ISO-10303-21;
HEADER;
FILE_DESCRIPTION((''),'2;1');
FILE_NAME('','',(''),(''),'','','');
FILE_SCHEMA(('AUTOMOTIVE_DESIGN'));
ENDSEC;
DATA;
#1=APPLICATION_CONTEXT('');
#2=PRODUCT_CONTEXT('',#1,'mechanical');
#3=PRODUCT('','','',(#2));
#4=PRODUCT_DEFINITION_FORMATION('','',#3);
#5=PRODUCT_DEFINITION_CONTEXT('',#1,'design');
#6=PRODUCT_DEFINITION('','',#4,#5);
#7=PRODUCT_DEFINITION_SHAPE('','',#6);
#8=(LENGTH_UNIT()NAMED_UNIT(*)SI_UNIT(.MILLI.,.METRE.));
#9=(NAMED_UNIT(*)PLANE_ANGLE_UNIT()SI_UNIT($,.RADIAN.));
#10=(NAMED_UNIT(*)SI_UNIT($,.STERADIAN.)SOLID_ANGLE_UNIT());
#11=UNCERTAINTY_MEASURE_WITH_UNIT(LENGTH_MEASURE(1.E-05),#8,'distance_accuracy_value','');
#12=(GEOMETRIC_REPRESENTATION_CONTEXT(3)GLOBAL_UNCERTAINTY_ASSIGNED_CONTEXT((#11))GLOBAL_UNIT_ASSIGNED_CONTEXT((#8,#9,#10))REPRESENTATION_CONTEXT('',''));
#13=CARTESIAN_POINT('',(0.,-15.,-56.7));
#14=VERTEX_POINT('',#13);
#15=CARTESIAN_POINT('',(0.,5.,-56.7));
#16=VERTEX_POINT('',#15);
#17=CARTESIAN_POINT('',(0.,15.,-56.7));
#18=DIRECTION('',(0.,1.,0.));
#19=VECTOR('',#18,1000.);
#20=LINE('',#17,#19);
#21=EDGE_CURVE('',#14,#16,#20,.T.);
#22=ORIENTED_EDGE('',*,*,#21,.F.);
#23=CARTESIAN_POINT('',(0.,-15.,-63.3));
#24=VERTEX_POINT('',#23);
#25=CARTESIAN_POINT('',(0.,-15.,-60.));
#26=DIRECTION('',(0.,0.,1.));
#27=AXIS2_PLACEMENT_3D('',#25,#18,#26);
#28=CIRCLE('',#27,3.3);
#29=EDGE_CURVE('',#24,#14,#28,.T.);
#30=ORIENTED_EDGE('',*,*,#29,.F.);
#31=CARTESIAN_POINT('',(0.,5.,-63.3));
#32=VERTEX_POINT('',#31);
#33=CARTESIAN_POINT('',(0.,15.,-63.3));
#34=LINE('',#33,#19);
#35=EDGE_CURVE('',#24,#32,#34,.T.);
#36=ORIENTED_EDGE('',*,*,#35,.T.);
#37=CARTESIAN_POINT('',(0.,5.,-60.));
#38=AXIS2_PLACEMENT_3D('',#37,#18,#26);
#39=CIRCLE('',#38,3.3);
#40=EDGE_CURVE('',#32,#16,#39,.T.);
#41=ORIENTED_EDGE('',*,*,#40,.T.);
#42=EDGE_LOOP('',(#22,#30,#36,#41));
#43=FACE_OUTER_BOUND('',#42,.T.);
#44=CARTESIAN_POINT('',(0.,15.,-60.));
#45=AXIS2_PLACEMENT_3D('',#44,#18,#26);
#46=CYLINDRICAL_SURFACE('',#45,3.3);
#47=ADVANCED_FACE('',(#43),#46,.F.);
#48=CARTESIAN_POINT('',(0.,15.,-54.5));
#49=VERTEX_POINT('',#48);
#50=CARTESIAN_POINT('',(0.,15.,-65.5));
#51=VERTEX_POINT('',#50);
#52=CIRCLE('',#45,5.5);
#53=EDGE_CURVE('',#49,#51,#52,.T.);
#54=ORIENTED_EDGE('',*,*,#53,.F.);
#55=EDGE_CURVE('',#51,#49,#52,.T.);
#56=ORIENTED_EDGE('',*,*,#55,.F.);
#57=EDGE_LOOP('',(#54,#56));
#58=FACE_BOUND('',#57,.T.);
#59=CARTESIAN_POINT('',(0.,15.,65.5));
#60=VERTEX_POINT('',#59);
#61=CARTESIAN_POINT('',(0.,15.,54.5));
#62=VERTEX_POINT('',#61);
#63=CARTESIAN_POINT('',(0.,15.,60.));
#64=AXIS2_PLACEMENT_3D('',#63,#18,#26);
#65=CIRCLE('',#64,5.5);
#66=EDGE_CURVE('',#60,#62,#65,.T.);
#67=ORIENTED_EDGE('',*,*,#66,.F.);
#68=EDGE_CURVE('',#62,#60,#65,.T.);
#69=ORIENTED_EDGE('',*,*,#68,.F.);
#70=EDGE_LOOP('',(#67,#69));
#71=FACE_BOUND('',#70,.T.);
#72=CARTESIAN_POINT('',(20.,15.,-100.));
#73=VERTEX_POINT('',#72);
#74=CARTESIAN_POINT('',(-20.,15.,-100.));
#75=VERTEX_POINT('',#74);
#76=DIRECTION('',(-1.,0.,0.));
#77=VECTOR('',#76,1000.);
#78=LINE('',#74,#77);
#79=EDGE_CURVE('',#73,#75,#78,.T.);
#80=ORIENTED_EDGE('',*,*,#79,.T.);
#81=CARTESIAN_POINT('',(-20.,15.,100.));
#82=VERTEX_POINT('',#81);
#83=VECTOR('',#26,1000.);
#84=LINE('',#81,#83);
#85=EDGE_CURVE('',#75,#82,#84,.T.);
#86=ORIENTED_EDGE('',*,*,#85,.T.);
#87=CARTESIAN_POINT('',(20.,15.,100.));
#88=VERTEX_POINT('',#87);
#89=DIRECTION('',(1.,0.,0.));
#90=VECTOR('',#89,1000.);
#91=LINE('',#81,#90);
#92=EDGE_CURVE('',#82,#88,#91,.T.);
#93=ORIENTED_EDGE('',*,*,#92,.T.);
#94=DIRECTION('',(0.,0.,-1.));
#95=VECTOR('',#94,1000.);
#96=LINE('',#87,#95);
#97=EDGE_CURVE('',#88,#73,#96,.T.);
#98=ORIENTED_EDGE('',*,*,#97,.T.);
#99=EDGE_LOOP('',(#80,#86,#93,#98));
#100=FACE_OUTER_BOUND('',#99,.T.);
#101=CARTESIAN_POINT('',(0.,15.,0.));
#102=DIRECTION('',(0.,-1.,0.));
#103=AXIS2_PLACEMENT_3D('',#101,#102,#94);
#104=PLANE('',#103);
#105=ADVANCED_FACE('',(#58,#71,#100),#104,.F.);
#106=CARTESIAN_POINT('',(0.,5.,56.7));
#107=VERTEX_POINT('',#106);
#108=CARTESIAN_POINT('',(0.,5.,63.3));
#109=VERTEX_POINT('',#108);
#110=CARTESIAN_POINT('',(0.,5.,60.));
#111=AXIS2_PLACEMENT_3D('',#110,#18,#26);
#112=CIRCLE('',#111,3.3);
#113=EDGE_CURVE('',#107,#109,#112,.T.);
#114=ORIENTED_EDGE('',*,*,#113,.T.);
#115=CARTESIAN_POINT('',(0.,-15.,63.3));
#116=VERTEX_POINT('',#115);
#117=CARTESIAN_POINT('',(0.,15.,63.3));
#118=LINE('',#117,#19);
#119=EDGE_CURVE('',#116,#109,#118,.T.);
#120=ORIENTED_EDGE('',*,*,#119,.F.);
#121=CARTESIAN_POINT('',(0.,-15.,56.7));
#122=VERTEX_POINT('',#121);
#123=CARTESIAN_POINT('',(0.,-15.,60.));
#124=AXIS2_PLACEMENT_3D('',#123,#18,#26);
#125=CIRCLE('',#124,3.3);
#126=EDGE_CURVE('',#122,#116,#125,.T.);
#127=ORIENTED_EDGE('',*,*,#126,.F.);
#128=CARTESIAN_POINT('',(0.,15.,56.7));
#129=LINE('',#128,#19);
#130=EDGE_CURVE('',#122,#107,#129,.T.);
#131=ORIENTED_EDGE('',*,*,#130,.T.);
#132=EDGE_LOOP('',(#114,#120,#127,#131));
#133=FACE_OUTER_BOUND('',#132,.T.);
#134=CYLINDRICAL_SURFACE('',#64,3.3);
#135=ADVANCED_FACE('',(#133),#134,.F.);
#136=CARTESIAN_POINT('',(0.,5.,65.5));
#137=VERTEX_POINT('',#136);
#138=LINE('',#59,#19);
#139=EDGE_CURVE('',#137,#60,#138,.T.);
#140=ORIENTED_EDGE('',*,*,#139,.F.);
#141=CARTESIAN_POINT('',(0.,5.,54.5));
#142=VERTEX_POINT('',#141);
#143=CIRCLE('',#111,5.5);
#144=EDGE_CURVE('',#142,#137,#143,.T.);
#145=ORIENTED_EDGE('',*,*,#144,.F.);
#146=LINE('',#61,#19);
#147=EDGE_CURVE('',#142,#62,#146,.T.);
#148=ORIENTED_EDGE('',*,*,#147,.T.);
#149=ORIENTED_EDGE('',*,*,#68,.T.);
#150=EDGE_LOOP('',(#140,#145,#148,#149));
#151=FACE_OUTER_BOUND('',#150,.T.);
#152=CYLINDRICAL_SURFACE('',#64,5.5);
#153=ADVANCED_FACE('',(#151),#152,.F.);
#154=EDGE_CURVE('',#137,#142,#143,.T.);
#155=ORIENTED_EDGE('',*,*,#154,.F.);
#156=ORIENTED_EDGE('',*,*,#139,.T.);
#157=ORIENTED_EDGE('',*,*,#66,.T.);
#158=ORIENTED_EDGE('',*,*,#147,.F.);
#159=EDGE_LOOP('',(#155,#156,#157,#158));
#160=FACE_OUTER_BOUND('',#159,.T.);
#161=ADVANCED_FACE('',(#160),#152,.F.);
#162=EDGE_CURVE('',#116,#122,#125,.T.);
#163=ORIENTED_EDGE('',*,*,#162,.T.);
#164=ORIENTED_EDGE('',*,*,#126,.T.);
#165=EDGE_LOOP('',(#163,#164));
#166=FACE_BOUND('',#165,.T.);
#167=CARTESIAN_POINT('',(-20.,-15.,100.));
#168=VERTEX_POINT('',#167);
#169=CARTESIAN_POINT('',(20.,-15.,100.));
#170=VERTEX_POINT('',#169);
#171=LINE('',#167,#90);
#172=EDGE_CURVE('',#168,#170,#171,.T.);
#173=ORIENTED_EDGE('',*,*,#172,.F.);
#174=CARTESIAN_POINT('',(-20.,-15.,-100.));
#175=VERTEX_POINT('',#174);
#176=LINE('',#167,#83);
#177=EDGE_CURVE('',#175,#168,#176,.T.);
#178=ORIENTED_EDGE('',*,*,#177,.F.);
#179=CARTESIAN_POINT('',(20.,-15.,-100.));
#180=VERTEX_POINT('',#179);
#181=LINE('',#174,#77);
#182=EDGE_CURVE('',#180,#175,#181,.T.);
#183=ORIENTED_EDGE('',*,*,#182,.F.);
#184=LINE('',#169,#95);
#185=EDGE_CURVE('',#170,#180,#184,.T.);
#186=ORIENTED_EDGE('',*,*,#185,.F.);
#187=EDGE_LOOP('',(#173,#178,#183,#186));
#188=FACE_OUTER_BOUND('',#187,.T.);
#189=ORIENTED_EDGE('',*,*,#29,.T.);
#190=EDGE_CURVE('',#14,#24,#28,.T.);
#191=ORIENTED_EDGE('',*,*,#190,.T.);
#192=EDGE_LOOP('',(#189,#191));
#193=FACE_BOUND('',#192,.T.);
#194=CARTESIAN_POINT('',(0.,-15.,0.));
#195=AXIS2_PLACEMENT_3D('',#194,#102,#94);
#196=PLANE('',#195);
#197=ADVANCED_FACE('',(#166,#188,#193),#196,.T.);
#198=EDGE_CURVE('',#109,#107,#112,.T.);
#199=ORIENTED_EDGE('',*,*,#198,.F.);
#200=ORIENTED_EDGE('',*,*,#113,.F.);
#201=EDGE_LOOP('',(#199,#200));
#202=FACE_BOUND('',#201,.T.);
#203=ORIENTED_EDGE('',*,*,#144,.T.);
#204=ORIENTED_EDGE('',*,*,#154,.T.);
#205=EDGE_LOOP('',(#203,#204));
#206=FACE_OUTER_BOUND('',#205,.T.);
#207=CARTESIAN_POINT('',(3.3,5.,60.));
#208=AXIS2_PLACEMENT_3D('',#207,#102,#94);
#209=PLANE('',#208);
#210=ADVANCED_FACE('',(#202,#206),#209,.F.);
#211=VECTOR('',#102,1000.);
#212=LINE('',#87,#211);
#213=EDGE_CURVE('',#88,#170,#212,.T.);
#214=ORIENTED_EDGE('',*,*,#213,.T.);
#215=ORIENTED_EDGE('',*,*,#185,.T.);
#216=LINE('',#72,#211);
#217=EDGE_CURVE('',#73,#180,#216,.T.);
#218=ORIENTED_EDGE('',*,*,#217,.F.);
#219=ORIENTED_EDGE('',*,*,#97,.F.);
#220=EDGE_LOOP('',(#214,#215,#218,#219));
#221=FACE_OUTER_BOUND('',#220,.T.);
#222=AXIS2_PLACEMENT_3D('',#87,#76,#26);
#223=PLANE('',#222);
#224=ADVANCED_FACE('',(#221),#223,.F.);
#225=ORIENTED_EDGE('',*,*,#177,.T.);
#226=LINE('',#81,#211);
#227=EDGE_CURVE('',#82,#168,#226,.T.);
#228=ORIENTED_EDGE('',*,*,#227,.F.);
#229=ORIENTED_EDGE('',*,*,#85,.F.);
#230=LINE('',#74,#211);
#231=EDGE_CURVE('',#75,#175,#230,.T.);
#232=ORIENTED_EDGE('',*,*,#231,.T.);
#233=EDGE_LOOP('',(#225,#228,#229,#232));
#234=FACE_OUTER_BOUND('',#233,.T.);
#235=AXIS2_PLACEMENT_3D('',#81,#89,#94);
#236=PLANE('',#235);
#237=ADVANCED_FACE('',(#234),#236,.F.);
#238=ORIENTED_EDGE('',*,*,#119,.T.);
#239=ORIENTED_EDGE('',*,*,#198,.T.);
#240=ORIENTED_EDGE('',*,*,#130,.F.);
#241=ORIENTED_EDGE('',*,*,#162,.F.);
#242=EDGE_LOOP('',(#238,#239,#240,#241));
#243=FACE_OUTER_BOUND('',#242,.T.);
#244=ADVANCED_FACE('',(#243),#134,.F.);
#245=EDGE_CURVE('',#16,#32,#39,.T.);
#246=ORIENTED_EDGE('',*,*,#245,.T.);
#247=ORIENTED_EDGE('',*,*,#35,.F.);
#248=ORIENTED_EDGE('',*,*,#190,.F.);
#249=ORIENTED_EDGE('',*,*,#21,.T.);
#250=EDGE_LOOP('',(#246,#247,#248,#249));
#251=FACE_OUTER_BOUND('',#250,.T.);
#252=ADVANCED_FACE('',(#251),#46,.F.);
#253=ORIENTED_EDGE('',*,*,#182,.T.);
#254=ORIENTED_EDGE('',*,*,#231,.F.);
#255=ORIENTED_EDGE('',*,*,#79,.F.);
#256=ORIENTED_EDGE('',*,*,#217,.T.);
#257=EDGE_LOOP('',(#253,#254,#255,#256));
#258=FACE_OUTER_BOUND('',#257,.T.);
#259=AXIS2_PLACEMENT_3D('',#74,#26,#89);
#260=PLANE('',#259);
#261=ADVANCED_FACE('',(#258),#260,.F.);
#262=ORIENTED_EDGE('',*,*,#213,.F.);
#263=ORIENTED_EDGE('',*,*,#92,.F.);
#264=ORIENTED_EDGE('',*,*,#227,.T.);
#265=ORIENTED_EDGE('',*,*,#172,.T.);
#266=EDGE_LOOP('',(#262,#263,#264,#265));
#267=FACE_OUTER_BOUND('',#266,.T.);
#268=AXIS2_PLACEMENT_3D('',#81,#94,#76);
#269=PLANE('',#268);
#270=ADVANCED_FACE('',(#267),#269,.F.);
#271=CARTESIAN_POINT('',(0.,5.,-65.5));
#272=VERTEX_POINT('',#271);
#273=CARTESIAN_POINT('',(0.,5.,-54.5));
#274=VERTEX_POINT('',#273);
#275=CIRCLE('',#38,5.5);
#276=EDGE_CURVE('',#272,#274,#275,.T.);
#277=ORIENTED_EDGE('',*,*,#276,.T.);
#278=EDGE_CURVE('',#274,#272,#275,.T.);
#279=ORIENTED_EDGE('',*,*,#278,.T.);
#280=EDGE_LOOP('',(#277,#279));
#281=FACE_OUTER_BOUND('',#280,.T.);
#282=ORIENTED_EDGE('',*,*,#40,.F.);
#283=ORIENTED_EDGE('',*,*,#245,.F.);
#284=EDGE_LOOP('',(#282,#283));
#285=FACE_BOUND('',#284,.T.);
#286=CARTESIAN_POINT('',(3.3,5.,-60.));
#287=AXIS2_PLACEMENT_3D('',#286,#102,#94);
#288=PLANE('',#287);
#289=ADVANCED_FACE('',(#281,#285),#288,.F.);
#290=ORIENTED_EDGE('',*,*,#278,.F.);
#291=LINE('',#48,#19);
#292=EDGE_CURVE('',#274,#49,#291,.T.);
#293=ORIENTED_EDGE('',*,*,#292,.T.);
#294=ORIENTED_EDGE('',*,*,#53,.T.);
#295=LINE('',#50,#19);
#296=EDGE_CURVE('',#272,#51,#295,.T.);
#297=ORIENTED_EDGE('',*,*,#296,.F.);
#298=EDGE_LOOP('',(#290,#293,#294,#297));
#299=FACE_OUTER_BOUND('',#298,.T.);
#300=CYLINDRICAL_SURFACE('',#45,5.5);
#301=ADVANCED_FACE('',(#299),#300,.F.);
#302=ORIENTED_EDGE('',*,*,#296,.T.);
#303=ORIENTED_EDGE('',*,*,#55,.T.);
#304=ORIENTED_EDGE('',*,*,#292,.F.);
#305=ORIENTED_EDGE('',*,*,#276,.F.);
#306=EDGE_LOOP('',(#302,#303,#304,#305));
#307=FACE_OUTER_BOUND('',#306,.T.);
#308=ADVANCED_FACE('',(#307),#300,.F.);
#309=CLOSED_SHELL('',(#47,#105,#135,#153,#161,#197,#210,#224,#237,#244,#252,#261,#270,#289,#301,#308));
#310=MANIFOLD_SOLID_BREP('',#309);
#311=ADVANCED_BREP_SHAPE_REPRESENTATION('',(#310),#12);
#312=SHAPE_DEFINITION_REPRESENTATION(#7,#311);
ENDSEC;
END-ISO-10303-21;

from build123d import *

# Parameters (mm, degrees)
SKETCH_1_W                = 40
SKETCH_1_H                = 200
EXTRUDE_1_DEPTH           = 15
HOLE_WIZARD_1_D           = 6.6
HOLE_WIZARD_1_CBORE_D     = 11
HOLE_WIZARD_1_CBORE_DEPTH = 10


with BuildPart() as part:
    # 草图1 → 凸台-拉伸1 (new, symmetric)
    with BuildSketch(Plane(origin=(0, 0, 0), x_dir=(1, 0, 0), z_dir=(0, 1, 0))):
        Rectangle(SKETCH_1_W, SKETCH_1_H)
    extrude(amount=EXTRUDE_1_DEPTH, both=True)

    # 打孔尺寸(%根据)内六角圆柱头螺钉的类型1 (through all)
    with Locations(Plane(origin=(0, 15, 0), x_dir=(1, 0, 0), z_dir=(0, 1, 0))):
        with Locations((0, 60), (0, -60)):
            CounterBoreHole(HOLE_WIZARD_1_D / 2, HOLE_WIZARD_1_CBORE_D / 2, HOLE_WIZARD_1_CBORE_DEPTH)


solid = part.part
